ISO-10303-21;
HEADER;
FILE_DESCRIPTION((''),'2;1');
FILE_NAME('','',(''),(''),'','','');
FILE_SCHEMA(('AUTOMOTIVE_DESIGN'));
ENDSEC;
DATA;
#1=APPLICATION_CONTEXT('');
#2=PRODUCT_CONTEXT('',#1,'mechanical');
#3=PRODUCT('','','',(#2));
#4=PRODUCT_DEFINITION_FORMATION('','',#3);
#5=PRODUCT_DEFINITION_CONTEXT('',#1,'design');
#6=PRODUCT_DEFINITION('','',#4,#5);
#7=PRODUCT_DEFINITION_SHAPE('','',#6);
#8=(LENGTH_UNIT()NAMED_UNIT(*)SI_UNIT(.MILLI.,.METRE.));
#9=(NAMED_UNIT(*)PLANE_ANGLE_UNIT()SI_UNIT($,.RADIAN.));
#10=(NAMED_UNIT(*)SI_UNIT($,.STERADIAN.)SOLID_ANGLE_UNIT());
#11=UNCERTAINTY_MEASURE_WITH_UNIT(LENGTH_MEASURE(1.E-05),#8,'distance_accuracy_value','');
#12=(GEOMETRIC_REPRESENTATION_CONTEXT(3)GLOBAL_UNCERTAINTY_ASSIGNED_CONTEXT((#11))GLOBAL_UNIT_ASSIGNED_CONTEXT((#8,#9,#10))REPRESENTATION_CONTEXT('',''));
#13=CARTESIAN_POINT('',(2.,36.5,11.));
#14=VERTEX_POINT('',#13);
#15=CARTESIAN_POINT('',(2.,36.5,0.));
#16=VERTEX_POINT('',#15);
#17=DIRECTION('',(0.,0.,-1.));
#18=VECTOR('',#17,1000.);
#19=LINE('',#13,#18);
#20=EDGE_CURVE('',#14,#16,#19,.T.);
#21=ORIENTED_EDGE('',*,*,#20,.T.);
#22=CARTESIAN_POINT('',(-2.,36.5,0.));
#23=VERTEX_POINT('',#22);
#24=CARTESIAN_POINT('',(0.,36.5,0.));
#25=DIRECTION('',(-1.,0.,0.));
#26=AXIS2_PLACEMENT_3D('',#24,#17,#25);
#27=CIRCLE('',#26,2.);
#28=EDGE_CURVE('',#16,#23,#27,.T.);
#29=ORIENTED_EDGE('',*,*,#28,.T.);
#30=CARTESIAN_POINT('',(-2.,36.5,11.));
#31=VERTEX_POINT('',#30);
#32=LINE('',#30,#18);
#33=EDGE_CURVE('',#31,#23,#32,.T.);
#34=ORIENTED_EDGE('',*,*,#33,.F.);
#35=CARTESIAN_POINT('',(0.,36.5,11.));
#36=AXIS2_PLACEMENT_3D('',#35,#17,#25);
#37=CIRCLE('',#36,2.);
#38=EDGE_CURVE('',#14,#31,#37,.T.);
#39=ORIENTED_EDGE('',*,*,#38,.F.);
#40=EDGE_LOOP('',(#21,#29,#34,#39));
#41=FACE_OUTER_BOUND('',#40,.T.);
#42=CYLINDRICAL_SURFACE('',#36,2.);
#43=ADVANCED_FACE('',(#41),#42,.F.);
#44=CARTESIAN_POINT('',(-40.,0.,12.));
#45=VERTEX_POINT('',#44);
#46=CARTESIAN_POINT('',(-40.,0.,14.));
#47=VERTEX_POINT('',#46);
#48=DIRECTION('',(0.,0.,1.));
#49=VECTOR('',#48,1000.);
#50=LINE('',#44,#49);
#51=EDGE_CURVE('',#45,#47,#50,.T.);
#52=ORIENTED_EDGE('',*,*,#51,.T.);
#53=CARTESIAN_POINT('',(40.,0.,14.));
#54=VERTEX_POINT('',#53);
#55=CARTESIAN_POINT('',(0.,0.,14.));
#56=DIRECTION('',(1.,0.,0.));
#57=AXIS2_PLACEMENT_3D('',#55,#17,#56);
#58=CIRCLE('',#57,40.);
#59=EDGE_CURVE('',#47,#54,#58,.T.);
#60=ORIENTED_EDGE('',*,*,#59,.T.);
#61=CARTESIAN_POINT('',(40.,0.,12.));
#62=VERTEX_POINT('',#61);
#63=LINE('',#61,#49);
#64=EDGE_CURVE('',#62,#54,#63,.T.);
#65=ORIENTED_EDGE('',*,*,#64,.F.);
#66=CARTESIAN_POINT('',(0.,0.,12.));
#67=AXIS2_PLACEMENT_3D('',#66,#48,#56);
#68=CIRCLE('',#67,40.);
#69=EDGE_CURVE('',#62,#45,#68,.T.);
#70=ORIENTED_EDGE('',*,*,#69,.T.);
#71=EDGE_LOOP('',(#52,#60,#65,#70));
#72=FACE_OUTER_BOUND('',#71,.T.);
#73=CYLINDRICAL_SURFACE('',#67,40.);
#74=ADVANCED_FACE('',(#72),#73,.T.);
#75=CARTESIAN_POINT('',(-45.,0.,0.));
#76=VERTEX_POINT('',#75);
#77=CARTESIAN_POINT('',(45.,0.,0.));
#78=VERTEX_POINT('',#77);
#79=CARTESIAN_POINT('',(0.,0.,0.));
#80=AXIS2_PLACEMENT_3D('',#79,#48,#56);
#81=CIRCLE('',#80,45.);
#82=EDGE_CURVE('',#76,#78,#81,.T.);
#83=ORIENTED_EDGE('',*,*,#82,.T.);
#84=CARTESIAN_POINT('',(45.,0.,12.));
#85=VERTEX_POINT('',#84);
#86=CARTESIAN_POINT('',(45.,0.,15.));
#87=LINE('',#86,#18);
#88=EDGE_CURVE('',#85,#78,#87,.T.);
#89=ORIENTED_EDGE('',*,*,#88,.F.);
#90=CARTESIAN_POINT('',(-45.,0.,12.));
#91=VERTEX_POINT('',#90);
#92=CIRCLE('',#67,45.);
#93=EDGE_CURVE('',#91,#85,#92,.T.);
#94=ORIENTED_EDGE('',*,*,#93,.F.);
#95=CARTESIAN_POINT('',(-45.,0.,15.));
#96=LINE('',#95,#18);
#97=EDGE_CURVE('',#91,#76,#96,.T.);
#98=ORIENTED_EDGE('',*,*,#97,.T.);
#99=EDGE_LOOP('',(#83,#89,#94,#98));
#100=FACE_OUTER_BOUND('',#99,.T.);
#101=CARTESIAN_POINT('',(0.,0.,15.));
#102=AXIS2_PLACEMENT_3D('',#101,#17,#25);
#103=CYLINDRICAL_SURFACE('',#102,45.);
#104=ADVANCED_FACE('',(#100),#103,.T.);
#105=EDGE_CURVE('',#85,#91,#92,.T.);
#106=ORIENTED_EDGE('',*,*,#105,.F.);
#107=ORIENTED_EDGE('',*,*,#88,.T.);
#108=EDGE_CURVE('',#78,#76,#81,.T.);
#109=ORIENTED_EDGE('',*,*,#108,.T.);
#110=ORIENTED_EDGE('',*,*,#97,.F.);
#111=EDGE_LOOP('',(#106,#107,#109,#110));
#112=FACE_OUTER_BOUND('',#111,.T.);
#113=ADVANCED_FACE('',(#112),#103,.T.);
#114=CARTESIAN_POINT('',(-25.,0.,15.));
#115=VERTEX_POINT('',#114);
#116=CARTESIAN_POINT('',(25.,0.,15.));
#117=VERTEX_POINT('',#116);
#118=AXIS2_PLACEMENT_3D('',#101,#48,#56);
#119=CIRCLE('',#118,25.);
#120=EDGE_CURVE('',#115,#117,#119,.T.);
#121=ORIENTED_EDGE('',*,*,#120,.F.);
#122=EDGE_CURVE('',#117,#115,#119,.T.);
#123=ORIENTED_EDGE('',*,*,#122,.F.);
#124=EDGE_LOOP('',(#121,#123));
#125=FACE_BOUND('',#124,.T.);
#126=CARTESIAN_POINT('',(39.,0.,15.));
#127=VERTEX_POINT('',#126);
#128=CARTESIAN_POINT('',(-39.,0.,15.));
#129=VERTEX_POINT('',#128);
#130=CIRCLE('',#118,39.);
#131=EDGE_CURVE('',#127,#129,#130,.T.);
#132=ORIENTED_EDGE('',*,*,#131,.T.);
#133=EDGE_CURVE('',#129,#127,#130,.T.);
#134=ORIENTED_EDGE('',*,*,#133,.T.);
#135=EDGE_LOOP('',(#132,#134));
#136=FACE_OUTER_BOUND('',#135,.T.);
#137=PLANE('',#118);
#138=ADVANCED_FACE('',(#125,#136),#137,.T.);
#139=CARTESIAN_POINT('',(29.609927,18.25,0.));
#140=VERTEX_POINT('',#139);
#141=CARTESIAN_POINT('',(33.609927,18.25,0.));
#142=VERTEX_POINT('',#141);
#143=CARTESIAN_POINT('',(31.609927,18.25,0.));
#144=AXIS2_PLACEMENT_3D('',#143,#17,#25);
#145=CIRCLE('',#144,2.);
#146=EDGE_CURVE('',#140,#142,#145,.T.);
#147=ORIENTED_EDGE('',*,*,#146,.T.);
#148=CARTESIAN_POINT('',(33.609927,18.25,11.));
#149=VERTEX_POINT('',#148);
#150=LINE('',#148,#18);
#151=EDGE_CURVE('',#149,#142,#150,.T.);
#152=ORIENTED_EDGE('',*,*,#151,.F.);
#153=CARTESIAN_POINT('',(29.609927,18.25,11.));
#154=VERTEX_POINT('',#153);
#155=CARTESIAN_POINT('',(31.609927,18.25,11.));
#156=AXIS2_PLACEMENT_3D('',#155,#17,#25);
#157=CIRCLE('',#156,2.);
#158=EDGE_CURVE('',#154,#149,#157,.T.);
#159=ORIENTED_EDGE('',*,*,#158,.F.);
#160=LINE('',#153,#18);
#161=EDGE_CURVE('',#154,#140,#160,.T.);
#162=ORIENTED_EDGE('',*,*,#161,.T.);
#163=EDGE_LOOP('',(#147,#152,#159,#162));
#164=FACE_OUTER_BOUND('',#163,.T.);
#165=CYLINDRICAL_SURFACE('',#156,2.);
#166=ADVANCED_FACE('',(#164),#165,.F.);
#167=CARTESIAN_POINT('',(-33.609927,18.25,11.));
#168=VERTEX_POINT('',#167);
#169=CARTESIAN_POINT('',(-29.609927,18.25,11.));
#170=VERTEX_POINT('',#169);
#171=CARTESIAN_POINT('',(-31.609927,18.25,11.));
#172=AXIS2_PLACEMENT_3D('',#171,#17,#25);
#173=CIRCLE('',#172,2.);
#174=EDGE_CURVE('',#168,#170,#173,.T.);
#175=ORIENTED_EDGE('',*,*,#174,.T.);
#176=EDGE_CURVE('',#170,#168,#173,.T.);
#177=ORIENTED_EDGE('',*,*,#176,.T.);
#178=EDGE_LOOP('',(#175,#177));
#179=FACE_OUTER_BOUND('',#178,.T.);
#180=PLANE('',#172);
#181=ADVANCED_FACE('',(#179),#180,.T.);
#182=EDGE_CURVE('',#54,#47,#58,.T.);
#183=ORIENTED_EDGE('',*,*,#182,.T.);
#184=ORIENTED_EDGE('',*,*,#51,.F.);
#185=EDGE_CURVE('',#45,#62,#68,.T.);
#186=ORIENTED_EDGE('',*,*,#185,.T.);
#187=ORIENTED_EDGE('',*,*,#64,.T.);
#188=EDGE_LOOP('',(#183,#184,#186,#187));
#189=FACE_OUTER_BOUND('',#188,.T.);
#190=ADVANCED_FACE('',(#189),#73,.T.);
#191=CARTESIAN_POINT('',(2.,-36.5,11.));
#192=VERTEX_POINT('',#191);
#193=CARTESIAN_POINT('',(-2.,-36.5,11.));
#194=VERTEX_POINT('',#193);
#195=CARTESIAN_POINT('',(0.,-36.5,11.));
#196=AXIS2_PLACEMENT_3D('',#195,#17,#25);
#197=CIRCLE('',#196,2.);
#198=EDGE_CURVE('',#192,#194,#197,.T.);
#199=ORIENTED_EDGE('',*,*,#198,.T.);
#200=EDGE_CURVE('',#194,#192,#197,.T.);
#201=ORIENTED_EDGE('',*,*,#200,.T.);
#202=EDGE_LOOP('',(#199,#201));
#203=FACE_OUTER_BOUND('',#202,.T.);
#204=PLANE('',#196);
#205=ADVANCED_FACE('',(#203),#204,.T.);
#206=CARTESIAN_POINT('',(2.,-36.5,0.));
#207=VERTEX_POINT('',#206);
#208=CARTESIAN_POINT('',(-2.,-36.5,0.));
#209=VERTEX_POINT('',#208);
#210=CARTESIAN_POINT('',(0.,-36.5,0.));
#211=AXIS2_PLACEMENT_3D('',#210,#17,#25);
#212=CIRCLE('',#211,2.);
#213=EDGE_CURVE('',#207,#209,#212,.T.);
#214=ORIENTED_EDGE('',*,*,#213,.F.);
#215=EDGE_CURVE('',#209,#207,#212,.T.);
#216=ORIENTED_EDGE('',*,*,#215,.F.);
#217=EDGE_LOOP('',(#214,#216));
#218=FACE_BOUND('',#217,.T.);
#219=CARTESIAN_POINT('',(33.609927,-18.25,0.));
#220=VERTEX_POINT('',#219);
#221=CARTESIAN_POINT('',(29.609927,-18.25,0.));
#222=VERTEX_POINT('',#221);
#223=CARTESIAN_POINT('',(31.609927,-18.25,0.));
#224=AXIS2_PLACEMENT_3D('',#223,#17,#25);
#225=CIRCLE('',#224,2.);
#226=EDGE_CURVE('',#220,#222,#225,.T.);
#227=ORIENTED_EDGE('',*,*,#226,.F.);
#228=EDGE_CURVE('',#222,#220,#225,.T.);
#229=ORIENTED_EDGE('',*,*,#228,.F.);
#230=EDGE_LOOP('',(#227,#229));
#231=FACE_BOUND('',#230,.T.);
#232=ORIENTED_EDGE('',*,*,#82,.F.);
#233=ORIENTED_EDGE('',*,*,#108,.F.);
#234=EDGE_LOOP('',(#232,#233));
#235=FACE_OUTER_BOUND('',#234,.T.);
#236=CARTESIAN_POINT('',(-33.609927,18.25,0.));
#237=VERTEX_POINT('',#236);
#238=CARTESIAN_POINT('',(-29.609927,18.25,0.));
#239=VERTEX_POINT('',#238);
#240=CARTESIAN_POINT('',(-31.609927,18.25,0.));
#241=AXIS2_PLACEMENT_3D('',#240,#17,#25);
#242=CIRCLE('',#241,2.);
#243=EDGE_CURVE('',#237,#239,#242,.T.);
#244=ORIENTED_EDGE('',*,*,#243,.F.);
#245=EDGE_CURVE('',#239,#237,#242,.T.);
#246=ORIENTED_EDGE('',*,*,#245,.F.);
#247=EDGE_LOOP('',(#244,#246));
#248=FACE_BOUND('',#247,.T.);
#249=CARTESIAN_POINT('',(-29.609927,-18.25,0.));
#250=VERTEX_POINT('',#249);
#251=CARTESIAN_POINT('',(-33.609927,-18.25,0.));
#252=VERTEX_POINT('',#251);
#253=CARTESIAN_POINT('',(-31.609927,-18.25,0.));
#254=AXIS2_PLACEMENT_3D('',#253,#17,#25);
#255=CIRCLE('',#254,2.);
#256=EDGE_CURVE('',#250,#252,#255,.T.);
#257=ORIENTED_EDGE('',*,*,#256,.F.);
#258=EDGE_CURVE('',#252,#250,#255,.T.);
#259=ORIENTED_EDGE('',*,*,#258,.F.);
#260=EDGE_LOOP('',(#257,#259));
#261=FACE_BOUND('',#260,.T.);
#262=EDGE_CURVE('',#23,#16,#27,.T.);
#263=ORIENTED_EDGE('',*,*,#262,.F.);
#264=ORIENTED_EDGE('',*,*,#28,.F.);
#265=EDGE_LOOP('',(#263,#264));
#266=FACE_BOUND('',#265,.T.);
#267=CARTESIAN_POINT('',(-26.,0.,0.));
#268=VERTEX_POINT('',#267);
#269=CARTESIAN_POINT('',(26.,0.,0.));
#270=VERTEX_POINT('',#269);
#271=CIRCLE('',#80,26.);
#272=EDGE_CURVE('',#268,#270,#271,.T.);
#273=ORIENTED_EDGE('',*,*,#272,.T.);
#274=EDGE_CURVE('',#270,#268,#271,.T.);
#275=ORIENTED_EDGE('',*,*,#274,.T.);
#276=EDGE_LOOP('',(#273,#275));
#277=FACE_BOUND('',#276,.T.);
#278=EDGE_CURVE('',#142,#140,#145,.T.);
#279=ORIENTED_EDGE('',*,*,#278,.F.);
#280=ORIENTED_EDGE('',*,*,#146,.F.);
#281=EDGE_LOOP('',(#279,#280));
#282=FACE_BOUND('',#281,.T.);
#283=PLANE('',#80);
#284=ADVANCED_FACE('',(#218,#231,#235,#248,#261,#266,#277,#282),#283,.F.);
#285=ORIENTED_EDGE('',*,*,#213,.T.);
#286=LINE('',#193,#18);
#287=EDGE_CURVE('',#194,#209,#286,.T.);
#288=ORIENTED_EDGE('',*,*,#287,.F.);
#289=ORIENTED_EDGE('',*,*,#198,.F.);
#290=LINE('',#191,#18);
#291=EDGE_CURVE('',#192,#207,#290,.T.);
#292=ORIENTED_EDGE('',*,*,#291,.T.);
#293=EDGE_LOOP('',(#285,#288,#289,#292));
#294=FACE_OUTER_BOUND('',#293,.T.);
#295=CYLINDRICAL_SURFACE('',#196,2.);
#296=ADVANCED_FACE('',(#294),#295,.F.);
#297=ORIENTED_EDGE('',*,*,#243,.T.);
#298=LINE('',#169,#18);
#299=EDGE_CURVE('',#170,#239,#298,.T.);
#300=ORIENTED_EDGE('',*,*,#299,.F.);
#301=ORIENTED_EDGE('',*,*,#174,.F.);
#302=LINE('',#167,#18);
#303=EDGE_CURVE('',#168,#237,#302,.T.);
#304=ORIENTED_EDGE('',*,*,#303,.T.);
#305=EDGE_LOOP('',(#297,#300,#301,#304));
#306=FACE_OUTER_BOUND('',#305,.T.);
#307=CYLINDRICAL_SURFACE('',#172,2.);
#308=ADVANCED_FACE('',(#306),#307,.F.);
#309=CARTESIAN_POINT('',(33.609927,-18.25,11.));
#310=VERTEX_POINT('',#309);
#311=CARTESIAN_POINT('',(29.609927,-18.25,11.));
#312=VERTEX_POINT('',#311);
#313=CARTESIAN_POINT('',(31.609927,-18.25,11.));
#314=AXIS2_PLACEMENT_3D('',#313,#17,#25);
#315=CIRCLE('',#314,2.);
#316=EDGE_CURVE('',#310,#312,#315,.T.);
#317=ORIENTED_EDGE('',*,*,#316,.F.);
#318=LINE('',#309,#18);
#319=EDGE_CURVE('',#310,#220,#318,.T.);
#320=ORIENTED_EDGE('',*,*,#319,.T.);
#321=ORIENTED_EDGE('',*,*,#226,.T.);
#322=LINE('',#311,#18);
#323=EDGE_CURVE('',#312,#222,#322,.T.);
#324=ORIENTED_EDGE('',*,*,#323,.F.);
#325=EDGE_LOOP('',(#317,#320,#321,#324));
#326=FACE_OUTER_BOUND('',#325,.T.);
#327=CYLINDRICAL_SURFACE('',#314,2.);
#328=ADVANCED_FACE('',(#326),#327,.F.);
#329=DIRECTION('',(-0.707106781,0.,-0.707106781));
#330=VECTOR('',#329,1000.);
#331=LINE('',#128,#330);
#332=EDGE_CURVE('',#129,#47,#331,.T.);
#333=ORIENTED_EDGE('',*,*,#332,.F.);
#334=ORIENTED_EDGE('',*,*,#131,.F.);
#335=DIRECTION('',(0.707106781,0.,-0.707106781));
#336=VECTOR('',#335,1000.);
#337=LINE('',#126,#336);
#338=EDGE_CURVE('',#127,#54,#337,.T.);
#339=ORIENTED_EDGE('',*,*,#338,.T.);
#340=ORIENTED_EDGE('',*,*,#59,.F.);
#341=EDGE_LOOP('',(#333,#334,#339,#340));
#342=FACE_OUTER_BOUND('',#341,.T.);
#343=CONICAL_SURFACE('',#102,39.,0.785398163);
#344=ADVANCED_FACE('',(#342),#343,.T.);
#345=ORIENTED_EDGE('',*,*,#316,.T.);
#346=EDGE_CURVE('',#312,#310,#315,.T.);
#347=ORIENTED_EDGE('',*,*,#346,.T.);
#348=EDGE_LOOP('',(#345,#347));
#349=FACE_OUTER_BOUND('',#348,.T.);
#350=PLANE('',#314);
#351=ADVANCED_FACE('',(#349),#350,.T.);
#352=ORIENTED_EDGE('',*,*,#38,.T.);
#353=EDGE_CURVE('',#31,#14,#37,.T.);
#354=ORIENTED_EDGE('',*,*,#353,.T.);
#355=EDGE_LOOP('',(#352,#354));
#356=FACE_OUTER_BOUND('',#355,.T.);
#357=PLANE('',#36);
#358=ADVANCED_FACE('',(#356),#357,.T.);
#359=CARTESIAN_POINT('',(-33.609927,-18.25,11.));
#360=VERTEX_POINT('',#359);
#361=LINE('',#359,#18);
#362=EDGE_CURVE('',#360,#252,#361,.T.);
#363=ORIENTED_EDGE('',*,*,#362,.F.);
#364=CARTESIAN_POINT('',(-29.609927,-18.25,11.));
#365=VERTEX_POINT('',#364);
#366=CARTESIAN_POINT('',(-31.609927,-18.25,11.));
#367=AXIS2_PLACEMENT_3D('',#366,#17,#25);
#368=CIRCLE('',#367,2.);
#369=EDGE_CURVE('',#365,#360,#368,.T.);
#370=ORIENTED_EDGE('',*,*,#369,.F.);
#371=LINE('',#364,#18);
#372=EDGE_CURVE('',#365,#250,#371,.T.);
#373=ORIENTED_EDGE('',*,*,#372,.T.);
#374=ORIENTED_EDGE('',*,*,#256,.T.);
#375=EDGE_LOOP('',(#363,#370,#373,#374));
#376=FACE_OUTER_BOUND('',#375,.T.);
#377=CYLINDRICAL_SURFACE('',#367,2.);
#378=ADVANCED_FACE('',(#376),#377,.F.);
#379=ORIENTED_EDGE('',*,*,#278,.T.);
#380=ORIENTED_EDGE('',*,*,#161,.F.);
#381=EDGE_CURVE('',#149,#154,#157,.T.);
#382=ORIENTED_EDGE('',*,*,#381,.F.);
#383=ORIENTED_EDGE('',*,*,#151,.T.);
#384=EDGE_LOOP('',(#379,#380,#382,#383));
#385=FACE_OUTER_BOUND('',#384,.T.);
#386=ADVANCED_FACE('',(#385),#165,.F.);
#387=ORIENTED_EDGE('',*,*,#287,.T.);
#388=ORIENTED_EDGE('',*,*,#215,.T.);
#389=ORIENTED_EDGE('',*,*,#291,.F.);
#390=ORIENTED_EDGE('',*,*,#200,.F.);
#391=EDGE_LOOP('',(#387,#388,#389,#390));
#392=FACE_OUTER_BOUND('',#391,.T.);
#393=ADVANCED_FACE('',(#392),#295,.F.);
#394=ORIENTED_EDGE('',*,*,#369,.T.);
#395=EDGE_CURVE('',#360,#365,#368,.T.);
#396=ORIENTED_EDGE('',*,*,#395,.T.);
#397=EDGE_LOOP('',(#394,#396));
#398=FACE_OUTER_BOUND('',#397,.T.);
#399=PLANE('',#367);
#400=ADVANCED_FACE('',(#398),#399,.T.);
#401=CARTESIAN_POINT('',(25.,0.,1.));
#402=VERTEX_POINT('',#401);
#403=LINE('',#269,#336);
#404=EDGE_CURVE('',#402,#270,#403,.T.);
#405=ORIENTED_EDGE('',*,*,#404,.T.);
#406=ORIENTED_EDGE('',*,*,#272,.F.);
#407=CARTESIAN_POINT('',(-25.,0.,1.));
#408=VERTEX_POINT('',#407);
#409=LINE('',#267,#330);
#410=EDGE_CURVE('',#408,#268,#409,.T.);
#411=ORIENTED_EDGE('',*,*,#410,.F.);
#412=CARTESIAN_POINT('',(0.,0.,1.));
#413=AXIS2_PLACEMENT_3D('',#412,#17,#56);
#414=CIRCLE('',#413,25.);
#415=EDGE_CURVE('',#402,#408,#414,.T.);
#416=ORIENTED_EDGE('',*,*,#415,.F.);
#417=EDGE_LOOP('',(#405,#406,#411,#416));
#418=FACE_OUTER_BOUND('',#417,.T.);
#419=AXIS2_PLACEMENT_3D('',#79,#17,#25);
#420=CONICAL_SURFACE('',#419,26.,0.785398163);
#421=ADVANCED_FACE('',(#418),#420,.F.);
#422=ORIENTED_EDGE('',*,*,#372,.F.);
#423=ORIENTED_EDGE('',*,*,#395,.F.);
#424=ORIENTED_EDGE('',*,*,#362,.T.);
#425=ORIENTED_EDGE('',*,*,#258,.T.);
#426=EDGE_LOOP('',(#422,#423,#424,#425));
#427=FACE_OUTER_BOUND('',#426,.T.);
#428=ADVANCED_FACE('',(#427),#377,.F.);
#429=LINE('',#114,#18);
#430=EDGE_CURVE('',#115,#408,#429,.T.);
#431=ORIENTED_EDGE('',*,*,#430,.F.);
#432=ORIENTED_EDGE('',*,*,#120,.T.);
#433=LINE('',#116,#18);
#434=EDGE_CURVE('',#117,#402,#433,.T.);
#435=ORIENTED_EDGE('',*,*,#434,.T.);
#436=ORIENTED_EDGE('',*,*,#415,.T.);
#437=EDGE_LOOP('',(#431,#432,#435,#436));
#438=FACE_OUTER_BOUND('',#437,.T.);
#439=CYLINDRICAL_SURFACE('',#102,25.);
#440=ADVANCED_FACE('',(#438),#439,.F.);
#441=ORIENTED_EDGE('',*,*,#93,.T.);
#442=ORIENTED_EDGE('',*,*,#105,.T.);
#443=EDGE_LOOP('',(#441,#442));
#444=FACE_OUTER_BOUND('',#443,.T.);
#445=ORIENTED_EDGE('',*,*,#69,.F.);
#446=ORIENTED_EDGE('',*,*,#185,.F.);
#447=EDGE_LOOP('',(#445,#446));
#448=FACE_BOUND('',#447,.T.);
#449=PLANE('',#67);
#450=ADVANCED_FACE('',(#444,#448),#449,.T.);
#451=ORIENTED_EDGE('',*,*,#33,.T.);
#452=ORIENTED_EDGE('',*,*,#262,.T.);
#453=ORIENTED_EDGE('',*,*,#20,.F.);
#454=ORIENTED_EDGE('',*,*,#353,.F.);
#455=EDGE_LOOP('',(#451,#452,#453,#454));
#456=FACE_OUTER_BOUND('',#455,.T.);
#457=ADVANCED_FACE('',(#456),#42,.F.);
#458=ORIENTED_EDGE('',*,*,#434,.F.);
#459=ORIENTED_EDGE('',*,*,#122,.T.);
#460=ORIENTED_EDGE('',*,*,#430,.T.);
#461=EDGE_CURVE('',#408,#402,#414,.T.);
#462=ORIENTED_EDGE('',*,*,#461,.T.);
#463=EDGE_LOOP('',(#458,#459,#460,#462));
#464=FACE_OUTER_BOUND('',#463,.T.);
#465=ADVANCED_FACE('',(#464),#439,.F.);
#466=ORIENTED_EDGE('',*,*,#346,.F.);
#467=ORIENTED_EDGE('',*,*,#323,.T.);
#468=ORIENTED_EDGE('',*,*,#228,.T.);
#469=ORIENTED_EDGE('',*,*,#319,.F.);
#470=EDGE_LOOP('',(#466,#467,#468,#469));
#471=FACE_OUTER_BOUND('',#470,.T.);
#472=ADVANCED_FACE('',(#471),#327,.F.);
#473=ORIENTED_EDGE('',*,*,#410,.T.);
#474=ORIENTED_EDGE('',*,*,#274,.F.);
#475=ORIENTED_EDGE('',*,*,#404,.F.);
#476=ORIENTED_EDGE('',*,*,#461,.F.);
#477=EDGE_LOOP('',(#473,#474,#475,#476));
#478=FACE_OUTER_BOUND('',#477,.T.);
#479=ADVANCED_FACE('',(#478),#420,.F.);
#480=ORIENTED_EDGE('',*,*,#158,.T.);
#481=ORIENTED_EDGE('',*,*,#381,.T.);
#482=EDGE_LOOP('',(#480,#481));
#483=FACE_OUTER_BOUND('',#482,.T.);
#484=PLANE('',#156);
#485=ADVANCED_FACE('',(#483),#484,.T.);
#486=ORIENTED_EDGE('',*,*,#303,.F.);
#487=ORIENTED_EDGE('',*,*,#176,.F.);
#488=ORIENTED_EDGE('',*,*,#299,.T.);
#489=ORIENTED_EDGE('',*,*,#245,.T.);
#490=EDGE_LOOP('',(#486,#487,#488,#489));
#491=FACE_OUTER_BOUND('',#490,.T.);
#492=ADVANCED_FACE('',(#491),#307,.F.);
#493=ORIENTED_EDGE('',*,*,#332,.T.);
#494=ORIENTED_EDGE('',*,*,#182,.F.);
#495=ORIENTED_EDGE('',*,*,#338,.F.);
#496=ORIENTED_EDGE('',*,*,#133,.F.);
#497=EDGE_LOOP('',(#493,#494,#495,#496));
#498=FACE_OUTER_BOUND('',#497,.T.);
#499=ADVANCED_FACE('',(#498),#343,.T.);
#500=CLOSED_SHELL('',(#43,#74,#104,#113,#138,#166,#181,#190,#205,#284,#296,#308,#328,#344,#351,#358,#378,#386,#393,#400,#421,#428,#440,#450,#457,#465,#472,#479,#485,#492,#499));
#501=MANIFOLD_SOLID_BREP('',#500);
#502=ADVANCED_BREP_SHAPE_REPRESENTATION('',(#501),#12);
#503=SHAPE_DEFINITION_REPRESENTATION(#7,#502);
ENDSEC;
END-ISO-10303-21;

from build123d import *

# Parameters (mm, degrees)
SKETCH1_R           = 45
SKETCH1_R_2         = 25
BOSS_EXTRUDE1_DEPTH = 15
CUT_EXTRUDE1_START  = -3
SKETCH2_R           = 45
SKETCH2_R_2         = 40
CUT_EXTRUDE1_DEPTH  = 3
SKETCH3_R           = 2
CUT_EXTRUDE2_DEPTH  = 11
CHAMFER1_SIZE       = 1


with BuildPart() as part:
    # Sketch1 → Boss-Extrude1 (new body)
    with BuildSketch(Plane.XY):
        Circle(SKETCH1_R)
        Circle(SKETCH1_R_2, mode=Mode.SUBTRACT)
    extrude(amount=BOSS_EXTRUDE1_DEPTH)

    # Sketch2 → Cut-Extrude1 (cut)
    with BuildSketch(Plane.XY.offset(15).offset(CUT_EXTRUDE1_START)):
        Circle(SKETCH2_R)
        Circle(SKETCH2_R_2, mode=Mode.SUBTRACT)
    extrude(amount=CUT_EXTRUDE1_DEPTH, mode=Mode.SUBTRACT)

    # Sketch3 → Cut-Extrude2 (cut)
    with BuildSketch(Plane(origin=(0, 0, 0), x_dir=(-1, 0, 0), z_dir=(0, 0, -1))):
        with Locations((0, 36.5)):
            Circle(SKETCH3_R)
        with Locations((31.609927238, 18.25)):
            Circle(SKETCH3_R)
        with Locations((31.609927238, -18.25)):
            Circle(SKETCH3_R)
        with Locations((0, -36.5)):
            Circle(SKETCH3_R)
        with Locations((-31.609927238, -18.25)):
            Circle(SKETCH3_R)
        with Locations((-31.609927238, 18.25)):
            Circle(SKETCH3_R)
    extrude(amount=-CUT_EXTRUDE2_DEPTH, mode=Mode.SUBTRACT)

    # Chamfer1
    chamfer1_edges = [part.edges().sort_by_distance(p)[0] for p in [
        (-40, 0, 15),
        (-25, 0, 0),
    ]]
    chamfer(chamfer1_edges, length=CHAMFER1_SIZE)


solid = part.part
